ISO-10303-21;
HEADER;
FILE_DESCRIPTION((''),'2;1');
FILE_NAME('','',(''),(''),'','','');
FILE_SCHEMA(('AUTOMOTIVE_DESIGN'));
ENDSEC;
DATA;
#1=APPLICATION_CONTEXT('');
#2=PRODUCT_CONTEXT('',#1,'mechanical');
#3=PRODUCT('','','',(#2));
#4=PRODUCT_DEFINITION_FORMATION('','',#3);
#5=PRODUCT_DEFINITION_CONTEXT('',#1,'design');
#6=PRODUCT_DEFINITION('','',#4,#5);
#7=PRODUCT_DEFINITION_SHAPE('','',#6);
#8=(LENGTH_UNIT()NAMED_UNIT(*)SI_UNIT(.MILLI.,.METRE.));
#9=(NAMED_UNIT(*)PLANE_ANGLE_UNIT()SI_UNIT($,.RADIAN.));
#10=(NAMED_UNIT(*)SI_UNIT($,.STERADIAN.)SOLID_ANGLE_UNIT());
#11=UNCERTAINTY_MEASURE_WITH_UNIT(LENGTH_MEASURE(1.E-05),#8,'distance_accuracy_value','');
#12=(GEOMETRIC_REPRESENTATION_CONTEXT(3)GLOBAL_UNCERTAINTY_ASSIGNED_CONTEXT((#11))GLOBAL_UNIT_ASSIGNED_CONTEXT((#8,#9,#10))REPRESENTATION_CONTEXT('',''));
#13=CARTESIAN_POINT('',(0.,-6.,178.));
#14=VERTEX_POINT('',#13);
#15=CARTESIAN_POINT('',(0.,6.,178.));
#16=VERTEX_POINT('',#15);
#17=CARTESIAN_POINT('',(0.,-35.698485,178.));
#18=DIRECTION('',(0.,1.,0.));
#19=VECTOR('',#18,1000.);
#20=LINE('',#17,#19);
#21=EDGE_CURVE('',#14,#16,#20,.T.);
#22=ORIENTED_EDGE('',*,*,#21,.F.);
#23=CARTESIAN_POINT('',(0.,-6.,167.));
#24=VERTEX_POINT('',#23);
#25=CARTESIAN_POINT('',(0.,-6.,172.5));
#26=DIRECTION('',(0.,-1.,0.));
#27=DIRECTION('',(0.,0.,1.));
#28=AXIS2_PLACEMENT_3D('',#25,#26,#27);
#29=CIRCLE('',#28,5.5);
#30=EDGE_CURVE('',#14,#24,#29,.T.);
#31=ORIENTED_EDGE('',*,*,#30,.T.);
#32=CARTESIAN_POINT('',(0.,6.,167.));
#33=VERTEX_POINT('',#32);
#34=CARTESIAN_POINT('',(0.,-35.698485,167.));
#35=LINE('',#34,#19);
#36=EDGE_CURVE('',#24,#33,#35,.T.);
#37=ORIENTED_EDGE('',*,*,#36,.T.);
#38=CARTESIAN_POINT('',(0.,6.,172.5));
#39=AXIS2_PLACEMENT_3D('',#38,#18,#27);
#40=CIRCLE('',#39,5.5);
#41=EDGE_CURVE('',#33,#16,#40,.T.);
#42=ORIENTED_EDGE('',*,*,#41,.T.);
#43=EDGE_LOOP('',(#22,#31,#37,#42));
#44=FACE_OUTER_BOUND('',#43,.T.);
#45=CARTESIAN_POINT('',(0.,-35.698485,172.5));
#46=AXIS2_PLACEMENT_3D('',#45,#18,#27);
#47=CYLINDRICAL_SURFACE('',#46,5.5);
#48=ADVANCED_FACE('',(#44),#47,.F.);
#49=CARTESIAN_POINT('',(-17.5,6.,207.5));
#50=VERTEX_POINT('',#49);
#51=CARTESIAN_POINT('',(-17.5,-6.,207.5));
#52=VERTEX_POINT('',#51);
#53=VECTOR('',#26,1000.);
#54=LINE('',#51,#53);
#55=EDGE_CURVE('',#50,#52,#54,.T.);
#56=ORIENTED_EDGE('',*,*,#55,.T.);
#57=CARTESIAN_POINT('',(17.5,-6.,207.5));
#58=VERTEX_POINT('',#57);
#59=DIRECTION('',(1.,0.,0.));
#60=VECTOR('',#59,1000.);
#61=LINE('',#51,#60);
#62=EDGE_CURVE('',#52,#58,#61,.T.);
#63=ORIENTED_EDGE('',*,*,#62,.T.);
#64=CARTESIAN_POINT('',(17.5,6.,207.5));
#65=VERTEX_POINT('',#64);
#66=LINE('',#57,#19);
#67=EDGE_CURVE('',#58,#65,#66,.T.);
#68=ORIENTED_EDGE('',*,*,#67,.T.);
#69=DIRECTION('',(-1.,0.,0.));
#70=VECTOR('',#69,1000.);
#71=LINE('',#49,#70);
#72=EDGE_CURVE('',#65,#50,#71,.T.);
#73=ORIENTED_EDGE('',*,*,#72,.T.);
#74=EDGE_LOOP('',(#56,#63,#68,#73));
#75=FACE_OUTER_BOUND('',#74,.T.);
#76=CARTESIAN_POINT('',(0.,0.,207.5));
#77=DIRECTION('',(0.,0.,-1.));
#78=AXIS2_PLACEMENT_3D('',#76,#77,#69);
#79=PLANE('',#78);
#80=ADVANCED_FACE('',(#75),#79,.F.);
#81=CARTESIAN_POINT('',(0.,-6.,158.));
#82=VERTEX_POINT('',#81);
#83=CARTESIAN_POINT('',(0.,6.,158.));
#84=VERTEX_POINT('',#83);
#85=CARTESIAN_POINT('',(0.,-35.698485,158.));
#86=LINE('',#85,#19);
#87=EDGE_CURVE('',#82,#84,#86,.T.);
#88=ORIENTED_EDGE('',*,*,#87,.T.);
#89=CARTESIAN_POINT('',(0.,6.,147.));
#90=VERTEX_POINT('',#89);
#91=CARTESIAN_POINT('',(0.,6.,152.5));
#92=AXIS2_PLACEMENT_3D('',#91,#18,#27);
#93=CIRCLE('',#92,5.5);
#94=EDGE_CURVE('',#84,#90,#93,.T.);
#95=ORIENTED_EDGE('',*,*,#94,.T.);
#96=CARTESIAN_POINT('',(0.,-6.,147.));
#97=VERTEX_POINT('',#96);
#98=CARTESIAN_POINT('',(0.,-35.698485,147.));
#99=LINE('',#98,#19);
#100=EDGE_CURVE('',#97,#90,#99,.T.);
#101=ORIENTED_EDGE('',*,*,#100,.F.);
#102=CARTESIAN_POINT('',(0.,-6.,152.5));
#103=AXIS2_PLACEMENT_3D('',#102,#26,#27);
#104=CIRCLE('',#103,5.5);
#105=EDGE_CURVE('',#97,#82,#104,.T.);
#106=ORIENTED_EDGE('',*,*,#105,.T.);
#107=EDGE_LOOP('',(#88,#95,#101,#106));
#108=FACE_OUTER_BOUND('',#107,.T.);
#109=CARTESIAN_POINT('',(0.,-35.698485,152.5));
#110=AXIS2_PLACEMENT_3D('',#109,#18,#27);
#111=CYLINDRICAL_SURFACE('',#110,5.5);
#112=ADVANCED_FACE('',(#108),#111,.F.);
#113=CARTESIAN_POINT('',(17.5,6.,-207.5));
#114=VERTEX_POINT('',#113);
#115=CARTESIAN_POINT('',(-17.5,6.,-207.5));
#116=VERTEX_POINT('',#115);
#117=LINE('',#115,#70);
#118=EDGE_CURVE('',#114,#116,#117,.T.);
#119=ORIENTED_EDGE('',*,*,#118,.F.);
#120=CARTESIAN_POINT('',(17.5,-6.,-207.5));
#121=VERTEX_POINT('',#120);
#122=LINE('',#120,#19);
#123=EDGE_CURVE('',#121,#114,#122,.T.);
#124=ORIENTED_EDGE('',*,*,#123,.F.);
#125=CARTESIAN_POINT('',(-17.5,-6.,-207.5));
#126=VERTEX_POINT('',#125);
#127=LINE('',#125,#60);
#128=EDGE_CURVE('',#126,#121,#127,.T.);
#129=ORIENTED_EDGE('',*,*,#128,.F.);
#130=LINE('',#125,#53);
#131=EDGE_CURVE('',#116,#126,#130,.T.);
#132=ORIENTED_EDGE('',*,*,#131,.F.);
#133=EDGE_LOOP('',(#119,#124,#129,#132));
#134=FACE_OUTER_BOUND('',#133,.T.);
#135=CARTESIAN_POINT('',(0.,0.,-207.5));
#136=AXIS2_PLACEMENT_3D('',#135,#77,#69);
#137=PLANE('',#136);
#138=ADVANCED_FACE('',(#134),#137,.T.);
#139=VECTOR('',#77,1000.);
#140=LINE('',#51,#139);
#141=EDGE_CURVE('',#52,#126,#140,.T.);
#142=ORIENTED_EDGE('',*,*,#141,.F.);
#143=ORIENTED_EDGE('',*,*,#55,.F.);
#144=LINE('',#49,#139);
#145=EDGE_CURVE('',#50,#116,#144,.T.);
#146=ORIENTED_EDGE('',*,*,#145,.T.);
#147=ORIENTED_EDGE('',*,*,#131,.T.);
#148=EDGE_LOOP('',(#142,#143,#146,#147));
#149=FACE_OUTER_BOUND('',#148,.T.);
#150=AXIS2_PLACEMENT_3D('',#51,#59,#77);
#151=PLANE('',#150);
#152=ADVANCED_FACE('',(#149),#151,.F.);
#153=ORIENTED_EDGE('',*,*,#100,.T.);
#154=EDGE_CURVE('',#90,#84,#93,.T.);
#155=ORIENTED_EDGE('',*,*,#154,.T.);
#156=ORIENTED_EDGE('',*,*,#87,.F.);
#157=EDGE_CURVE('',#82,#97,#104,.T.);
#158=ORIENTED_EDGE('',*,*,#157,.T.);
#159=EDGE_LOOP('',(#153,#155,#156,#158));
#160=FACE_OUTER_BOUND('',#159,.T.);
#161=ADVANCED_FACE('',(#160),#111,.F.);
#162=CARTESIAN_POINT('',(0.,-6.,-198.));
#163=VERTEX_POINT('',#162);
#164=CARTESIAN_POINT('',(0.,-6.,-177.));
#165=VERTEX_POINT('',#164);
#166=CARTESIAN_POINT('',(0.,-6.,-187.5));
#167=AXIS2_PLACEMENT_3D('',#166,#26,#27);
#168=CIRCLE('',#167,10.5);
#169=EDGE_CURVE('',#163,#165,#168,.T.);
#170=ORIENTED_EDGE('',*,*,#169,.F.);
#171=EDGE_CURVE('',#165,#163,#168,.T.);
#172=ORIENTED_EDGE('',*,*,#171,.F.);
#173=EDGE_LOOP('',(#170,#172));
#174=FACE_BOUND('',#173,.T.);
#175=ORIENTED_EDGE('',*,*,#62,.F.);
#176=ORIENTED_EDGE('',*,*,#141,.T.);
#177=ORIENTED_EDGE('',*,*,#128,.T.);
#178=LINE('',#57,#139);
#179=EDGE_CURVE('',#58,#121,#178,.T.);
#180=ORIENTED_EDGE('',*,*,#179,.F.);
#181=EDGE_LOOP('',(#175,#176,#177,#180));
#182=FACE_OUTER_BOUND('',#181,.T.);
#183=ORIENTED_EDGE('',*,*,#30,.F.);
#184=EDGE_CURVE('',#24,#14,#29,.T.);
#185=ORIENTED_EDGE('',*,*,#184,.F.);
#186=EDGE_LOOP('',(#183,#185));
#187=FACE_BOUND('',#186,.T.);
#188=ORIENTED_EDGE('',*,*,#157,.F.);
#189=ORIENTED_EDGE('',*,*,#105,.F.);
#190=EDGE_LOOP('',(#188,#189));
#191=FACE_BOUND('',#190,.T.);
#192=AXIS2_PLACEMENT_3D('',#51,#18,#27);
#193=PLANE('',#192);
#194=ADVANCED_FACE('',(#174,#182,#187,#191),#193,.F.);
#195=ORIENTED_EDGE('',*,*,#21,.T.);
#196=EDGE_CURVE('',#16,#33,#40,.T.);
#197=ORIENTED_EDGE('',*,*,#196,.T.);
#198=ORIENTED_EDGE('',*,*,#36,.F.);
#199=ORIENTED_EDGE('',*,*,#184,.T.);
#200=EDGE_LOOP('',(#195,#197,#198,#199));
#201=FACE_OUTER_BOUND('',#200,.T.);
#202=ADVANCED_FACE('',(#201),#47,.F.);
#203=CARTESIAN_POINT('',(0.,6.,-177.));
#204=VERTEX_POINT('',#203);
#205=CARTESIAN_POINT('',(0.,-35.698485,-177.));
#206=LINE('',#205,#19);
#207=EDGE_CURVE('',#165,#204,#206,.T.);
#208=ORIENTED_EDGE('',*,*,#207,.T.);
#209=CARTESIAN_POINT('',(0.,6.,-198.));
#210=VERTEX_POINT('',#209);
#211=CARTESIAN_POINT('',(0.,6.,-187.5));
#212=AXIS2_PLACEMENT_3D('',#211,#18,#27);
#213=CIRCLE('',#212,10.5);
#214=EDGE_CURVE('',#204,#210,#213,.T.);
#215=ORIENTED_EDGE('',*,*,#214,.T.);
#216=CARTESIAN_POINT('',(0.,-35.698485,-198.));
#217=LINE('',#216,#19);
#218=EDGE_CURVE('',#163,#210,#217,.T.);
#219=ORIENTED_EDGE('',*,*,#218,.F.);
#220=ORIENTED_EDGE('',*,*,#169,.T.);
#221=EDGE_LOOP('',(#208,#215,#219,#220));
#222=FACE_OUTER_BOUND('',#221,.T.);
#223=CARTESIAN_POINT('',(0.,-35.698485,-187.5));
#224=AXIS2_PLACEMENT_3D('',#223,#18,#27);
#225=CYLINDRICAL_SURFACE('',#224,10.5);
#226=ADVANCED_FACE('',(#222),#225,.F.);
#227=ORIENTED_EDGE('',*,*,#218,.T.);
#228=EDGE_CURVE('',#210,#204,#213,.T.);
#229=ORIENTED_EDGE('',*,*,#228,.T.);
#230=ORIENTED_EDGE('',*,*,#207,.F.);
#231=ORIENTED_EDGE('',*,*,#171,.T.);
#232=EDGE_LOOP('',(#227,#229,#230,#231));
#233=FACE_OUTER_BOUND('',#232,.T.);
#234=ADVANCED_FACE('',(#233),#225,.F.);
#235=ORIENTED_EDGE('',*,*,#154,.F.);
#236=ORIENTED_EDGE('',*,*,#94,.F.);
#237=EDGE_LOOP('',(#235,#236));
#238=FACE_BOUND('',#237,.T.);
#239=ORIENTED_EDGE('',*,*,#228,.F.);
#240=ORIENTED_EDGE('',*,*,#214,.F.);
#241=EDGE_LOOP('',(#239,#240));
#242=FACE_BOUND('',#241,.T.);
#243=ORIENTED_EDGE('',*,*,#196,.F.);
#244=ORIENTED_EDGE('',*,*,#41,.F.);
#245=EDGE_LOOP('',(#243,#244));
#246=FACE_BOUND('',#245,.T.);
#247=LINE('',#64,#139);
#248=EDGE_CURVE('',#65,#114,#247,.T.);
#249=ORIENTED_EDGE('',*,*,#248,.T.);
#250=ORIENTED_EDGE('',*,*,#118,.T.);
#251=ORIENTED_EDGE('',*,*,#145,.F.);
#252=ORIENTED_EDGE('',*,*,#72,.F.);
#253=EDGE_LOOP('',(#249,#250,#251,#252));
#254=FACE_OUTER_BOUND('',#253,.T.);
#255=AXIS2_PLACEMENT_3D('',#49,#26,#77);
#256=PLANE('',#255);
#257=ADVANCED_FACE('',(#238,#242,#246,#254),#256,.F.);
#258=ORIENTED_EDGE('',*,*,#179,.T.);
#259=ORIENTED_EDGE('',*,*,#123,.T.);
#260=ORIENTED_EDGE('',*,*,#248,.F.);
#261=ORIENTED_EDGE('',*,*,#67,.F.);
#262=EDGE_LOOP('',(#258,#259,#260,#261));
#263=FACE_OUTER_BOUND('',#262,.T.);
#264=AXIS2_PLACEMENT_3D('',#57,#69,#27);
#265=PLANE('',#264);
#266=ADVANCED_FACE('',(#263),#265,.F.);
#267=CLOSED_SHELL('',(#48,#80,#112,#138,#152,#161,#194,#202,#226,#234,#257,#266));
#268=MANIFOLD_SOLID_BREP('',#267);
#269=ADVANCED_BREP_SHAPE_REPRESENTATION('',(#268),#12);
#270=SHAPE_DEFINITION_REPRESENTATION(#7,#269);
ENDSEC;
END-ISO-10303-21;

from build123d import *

# Parameters (mm, degrees)
SKETCH_1_W          = 35
SKETCH_1_H          = 12
EXTRUDE_1_DEPTH     = 207.5
SKETCH_2_R          = 10.5
SKETCH_2_R_2        = 5.5
CUT_EXTRUDE_1_DEPTH = 12


with BuildPart() as part:
    # 草图1 → 凸台-拉伸1 (new, symmetric)
    with BuildSketch(Plane.XY):
        Rectangle(SKETCH_1_W, SKETCH_1_H)
    extrude(amount=EXTRUDE_1_DEPTH, both=True)

    # 草图2 → 切除-拉伸1 (cut)
    with BuildSketch(Plane(origin=(0, 6, 0), x_dir=(1, 0, 0), z_dir=(0, 1, 0))):
        with Locations(Location((0, 187.5, 0), (0, 0, 270))):
            Circle(SKETCH_2_R)
        with Locations(Location((0, -152.5, 0), (0, 0, 270))):
            Circle(SKETCH_2_R_2)
        with Locations(Location((0, -172.5, 0), (0, 0, 270))):
            Circle(SKETCH_2_R_2)
    extrude(amount=-CUT_EXTRUDE_1_DEPTH, mode=Mode.SUBTRACT)


solid = part.part
